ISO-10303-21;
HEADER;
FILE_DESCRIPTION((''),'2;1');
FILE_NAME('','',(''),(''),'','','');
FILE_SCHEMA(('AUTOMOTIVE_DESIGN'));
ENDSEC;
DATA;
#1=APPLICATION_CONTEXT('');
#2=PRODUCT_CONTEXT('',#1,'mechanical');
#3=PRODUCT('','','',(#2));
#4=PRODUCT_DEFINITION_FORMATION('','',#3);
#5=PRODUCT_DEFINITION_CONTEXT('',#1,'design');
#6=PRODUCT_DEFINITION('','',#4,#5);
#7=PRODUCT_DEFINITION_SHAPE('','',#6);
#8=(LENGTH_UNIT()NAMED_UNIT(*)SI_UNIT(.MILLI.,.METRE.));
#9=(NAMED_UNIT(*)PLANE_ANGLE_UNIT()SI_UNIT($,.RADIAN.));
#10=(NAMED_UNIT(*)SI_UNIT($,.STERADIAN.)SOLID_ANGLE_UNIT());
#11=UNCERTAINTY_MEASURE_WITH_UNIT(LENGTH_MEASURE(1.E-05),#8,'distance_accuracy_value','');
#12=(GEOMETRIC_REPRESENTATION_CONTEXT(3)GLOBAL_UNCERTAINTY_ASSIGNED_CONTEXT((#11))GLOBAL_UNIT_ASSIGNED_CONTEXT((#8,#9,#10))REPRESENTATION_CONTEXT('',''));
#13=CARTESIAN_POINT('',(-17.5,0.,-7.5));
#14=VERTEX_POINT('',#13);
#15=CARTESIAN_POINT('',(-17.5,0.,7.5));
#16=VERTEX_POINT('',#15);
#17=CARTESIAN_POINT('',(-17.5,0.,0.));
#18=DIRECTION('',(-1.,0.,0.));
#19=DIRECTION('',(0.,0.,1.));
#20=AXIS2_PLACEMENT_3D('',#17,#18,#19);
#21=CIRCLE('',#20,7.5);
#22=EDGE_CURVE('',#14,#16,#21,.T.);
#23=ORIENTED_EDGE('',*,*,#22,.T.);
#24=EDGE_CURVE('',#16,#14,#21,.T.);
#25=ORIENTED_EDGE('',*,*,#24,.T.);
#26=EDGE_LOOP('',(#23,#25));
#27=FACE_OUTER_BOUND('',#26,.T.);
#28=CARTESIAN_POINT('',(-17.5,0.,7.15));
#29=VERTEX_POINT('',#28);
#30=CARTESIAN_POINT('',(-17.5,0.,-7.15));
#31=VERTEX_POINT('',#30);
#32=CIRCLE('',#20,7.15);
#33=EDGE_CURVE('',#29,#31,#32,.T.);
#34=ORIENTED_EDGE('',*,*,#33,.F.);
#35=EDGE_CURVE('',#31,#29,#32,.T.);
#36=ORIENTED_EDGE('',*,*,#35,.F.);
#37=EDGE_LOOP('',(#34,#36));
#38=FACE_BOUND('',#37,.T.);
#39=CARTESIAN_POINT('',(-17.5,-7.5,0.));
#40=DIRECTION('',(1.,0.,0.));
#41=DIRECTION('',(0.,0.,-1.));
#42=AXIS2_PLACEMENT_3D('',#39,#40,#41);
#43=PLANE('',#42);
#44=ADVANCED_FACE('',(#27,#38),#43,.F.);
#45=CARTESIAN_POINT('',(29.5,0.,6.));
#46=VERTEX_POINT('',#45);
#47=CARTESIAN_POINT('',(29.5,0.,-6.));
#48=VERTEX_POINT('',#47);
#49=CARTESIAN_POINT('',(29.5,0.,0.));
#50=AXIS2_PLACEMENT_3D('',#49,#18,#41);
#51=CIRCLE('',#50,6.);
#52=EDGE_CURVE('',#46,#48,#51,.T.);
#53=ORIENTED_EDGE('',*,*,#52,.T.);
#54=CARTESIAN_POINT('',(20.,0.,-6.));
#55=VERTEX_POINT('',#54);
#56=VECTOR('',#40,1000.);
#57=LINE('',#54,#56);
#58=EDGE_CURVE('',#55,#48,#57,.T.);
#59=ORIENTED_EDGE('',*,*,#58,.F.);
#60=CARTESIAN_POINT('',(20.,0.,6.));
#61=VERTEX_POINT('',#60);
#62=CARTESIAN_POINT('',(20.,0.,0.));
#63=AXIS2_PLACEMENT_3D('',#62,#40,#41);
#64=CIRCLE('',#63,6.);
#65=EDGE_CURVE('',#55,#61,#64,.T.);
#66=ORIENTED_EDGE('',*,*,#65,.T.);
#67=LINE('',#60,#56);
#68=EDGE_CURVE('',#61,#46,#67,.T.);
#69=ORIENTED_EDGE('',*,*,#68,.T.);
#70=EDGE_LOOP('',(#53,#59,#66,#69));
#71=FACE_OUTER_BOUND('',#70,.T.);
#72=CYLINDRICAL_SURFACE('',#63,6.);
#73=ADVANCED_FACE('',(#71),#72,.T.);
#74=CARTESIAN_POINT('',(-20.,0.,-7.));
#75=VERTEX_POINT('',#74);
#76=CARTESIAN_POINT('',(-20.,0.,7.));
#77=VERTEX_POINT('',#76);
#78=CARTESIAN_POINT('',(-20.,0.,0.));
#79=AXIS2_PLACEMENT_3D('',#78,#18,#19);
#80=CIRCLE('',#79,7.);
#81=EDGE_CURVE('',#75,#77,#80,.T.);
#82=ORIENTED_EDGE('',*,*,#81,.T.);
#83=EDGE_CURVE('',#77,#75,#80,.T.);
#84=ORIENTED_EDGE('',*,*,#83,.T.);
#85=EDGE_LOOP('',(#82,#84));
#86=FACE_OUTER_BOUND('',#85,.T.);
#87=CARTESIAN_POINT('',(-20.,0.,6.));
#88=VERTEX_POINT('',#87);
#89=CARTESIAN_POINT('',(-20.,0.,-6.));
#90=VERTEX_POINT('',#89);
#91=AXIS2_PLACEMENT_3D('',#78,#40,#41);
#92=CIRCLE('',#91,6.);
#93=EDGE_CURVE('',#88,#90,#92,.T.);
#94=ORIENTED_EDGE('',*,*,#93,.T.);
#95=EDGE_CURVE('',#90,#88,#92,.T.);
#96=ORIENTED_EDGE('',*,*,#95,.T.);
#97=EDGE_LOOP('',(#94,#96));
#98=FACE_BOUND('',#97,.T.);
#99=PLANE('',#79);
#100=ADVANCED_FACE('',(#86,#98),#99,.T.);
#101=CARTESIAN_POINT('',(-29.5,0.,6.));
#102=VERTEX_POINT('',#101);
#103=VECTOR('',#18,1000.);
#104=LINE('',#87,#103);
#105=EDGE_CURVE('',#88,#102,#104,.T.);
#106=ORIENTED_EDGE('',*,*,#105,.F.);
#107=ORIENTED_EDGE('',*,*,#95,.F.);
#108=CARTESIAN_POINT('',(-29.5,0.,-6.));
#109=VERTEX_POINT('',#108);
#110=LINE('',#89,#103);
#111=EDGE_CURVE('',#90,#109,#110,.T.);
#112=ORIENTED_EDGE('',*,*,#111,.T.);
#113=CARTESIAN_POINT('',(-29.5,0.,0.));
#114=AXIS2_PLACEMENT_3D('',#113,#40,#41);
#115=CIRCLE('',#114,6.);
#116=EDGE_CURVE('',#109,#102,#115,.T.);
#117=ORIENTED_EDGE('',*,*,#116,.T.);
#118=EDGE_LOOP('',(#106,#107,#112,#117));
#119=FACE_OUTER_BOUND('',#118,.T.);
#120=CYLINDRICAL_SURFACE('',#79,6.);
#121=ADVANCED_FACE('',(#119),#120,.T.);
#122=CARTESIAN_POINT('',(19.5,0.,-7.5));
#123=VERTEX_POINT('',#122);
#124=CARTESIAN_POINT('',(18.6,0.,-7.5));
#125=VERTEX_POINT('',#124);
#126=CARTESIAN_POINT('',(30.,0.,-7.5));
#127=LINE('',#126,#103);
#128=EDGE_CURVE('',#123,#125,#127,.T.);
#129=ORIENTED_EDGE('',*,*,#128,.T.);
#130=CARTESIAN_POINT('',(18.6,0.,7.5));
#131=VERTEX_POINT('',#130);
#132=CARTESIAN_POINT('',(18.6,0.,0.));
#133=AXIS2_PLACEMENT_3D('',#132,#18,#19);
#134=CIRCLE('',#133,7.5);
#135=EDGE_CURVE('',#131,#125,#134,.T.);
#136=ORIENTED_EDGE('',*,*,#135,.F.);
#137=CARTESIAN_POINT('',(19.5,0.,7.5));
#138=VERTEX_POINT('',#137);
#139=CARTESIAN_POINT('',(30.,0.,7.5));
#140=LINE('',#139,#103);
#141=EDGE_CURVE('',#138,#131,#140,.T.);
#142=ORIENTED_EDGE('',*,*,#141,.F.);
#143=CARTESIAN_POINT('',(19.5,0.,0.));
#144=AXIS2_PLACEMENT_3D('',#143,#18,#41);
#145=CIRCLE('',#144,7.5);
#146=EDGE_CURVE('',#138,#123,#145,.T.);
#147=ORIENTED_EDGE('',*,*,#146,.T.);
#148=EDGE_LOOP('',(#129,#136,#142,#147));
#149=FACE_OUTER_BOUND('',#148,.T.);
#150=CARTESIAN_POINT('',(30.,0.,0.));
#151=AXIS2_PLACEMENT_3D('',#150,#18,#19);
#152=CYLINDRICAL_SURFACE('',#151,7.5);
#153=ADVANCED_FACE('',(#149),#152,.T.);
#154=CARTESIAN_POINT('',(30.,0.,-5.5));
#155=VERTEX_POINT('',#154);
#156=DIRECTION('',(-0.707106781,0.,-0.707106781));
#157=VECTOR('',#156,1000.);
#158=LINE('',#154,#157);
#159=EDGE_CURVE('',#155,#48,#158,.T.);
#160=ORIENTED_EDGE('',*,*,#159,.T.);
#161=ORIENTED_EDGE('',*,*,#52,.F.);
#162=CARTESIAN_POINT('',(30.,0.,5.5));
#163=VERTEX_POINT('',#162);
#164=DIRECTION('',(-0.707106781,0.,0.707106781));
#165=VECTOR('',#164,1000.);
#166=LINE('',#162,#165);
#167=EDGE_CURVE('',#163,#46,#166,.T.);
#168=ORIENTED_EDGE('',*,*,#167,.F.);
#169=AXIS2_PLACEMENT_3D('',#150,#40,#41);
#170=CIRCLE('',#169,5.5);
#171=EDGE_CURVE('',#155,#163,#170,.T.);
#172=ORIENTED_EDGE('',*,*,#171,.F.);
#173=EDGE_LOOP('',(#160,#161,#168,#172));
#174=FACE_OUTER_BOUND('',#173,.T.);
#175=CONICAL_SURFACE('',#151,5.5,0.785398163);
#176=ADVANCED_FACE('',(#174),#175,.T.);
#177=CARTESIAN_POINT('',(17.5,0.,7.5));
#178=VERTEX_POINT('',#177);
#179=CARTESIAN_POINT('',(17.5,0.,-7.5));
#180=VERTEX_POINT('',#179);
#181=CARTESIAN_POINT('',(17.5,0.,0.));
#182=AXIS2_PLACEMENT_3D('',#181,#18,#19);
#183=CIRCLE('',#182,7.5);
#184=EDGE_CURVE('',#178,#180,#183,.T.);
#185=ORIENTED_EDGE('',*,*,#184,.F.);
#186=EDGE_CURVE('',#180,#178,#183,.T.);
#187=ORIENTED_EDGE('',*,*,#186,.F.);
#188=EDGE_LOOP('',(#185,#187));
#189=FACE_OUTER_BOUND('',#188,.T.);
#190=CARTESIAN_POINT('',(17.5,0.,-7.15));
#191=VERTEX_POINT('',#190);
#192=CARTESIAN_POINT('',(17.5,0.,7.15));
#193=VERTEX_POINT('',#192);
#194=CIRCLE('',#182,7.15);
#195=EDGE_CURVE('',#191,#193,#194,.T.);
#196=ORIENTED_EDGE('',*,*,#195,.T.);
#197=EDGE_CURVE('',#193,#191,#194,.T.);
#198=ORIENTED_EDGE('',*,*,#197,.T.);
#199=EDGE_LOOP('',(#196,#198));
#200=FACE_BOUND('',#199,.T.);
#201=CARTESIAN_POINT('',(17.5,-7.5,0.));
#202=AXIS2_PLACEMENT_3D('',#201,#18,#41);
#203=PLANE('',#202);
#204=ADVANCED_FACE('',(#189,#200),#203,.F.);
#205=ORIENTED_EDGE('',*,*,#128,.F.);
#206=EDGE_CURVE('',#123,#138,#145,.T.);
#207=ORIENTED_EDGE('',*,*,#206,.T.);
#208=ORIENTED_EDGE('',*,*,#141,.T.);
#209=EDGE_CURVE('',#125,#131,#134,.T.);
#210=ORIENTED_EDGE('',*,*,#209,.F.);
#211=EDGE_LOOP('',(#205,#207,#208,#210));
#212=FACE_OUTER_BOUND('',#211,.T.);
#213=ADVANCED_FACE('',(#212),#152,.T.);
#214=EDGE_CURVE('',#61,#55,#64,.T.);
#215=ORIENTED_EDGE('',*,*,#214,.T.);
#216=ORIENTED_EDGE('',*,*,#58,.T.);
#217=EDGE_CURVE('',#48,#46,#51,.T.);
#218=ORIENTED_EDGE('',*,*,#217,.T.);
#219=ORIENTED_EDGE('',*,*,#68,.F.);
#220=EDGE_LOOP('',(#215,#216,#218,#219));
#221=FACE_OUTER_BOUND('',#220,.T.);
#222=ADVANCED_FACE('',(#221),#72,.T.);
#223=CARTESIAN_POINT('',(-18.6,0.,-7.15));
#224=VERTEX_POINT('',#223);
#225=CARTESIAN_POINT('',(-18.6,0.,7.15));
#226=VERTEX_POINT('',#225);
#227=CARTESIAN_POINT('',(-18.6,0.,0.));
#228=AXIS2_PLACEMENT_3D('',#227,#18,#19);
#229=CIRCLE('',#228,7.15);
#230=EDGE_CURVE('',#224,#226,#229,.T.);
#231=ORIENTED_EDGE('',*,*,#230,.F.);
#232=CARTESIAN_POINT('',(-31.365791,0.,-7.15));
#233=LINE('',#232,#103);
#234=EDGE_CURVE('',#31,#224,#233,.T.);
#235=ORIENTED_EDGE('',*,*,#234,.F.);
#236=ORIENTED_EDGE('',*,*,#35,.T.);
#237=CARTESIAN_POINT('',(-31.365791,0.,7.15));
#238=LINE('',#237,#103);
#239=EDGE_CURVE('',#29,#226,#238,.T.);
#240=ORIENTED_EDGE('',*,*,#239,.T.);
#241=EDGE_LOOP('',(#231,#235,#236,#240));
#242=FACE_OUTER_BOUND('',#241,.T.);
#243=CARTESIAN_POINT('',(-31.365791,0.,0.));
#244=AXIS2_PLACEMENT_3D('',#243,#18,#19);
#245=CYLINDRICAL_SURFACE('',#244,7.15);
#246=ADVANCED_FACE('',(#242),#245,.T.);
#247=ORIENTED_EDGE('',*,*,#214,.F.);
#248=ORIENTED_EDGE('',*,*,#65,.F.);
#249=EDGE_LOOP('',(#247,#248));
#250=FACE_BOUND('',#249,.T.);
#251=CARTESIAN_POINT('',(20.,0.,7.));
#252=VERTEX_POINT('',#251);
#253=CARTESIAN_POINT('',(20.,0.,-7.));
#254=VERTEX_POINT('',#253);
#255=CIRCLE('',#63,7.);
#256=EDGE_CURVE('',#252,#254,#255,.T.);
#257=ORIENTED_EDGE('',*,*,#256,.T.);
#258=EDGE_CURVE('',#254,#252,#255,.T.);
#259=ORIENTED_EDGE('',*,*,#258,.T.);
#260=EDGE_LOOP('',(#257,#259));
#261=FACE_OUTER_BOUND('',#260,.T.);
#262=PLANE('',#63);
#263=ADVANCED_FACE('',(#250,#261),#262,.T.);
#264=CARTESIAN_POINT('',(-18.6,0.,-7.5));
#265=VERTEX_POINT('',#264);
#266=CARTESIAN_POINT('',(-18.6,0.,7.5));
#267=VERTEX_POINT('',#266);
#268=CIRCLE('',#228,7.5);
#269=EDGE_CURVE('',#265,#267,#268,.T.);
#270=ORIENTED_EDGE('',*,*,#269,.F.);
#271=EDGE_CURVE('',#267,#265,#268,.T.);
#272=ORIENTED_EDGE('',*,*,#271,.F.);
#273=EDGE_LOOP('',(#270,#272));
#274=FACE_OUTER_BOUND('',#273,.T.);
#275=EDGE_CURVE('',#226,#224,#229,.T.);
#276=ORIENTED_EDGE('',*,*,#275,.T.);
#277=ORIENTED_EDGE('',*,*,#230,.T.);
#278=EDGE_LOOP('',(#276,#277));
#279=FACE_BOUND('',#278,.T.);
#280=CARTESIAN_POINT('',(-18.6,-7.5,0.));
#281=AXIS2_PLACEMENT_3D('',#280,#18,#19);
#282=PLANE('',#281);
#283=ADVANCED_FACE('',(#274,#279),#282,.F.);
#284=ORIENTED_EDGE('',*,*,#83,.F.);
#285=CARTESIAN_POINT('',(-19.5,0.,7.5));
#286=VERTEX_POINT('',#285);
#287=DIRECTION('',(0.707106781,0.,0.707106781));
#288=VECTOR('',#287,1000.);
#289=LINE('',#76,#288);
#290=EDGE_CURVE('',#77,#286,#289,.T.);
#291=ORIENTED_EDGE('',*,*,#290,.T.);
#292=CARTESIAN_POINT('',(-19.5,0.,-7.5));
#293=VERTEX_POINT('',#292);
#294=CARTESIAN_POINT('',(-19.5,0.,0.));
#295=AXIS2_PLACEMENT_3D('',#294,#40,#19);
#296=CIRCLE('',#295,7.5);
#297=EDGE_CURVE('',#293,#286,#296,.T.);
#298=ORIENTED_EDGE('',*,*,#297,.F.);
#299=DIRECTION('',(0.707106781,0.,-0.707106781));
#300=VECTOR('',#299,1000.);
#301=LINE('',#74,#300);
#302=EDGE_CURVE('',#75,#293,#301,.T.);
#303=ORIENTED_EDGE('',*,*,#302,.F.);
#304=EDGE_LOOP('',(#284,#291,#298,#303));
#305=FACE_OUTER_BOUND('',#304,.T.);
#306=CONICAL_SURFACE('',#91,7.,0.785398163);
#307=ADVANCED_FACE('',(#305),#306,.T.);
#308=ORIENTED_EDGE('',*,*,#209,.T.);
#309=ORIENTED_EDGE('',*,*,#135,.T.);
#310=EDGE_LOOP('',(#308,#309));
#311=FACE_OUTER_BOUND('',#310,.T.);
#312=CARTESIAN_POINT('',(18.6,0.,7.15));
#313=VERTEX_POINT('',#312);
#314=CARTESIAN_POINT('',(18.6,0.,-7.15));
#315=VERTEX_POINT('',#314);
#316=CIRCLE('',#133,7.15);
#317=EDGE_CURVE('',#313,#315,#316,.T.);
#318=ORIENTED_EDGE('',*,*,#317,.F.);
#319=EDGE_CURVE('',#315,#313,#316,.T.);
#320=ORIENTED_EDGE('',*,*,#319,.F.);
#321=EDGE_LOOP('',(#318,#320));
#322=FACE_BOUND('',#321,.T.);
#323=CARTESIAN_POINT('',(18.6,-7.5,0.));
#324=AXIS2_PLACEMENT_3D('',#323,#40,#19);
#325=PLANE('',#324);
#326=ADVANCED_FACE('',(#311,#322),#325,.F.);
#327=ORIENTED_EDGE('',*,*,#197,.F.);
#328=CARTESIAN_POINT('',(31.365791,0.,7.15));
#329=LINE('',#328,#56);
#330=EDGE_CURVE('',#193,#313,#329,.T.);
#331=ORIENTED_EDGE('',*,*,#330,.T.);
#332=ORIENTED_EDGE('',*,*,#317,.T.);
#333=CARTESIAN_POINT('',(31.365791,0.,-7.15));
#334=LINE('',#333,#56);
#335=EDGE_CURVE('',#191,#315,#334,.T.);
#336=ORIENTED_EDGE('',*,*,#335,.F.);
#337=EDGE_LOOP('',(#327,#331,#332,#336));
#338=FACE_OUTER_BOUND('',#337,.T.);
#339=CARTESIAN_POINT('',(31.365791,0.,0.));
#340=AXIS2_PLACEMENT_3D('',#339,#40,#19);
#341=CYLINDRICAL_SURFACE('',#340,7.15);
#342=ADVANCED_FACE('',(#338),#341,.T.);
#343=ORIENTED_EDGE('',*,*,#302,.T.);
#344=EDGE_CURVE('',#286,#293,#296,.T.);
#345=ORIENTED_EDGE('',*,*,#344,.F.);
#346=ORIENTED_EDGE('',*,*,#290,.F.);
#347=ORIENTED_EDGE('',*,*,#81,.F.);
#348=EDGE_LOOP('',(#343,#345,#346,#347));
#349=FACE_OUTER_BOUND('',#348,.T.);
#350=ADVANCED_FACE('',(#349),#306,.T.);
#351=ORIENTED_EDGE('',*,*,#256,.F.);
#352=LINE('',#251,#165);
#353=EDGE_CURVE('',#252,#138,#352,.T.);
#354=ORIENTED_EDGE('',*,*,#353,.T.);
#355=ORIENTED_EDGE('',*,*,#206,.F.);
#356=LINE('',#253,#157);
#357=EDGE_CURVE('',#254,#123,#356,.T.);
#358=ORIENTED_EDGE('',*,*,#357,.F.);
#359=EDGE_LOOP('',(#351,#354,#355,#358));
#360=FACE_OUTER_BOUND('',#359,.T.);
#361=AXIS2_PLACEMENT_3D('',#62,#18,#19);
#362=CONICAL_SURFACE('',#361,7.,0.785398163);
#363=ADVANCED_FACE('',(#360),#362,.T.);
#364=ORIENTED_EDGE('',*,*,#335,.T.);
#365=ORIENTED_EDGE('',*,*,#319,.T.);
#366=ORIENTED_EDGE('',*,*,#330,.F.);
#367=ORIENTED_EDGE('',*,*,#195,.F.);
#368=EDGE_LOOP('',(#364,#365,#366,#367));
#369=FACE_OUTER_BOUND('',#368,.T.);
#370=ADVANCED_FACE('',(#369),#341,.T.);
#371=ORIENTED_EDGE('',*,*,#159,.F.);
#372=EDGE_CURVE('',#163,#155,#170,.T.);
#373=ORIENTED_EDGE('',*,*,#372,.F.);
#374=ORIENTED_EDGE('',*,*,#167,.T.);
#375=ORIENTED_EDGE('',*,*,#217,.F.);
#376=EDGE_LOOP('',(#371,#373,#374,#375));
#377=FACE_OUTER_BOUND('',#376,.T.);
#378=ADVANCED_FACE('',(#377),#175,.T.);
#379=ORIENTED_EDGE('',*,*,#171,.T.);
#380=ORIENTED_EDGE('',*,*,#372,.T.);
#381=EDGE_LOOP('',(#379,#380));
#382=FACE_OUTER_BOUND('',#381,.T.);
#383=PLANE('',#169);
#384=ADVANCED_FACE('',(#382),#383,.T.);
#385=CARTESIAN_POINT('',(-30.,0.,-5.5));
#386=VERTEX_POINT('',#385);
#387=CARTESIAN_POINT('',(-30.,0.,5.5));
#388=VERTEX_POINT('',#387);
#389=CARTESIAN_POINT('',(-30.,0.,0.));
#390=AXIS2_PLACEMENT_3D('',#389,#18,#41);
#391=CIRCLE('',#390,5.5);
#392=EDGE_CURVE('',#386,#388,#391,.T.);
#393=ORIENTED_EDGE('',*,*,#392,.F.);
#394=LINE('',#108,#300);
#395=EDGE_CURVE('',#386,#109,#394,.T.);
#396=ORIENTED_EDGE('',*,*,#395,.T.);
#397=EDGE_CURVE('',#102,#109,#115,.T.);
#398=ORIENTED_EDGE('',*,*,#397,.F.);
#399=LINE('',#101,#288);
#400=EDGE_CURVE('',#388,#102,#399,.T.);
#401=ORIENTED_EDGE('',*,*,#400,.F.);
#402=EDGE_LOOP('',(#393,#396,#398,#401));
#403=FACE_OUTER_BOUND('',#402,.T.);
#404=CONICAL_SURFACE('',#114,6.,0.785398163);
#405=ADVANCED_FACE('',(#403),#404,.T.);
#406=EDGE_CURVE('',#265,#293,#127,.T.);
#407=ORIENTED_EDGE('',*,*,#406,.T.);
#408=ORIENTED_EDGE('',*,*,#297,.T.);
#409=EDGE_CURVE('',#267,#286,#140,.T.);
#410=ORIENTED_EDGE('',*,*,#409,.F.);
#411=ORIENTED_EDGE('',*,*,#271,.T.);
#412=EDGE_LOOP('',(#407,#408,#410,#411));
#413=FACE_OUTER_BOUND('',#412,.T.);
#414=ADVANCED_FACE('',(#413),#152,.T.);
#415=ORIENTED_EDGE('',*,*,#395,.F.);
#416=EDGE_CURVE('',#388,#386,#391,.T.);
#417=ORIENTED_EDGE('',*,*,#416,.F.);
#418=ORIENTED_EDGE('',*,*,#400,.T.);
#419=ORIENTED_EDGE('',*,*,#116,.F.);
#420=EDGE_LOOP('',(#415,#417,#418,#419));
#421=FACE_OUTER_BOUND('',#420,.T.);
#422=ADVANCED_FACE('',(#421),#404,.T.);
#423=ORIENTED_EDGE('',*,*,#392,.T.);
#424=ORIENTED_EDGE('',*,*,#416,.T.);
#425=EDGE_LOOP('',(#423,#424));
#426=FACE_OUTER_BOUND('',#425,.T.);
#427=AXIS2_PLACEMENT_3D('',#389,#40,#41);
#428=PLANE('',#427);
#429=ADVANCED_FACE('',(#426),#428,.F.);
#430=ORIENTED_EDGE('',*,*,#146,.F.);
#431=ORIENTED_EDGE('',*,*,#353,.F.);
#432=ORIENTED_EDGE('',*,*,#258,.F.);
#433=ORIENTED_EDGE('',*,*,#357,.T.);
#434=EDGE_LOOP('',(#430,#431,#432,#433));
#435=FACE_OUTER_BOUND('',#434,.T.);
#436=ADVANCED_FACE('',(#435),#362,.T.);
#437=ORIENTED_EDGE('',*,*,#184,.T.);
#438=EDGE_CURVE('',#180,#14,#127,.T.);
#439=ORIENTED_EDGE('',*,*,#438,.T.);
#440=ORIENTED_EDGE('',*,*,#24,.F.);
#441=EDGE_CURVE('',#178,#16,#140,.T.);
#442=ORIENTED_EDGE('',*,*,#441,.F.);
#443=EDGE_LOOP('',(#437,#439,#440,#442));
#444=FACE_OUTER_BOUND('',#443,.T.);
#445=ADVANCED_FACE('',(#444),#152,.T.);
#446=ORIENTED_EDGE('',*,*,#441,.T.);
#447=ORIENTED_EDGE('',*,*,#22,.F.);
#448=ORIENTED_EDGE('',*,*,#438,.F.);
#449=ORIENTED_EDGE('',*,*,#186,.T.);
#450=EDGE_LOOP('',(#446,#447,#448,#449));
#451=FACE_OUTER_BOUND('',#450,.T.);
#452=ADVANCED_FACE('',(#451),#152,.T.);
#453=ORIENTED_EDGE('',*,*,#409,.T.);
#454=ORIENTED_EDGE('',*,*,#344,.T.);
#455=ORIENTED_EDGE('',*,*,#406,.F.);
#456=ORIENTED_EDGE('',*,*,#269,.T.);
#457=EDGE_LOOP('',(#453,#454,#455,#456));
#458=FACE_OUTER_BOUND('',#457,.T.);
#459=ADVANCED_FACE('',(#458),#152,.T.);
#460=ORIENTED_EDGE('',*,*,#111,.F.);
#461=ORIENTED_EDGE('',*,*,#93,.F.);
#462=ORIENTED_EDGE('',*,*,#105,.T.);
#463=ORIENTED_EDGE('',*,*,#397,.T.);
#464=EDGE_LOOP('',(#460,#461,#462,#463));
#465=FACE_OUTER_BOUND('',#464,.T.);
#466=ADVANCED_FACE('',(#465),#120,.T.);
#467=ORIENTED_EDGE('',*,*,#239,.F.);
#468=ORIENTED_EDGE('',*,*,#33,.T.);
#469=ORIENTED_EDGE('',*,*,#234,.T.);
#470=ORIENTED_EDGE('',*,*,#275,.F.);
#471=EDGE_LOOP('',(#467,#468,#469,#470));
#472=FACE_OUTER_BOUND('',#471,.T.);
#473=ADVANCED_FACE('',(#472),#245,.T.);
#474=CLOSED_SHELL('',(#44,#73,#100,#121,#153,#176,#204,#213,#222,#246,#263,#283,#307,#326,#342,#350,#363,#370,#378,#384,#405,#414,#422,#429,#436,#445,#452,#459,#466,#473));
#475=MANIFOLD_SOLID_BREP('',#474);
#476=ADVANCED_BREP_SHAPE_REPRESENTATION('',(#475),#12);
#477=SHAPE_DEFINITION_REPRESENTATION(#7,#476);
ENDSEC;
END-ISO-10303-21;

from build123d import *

# Parameters (mm, degrees)
SKETCH_1_R          = 7.5
EXTRUDE_1_DEPTH     = 30
SKETCH_2_OUTSIDE_W  = 29.728
SKETCH_2_OUTSIDE_H  = 29.728
SKETCH_2_OUTSIDE_R  = 6
CUT_EXTRUDE_1_DEPTH = 10
CHAMFER_1_SIZE      = 0.5
SKETCH_3_W          = 1.1
SKETCH_3_H          = 0.35


with BuildPart() as part:
    # 草图1 → 凸台-拉伸1 (new, symmetric)
    with BuildSketch(Plane(origin=(0, 0, 0), x_dir=(0, 0, -1), z_dir=(1, 0, 0))):
        Circle(SKETCH_1_R)
    extrude(amount=EXTRUDE_1_DEPTH, both=True)

    # 草图2 outside → 切除-拉伸1 (cut)
    with BuildSketch(Plane(origin=(30, 0, 0), x_dir=(0, 0, -1), z_dir=(1, 0, 0))):
        Rectangle(SKETCH_2_OUTSIDE_W, SKETCH_2_OUTSIDE_H)
        Circle(SKETCH_2_OUTSIDE_R, mode=Mode.SUBTRACT)
    cut_extrude_1 = extrude(amount=-CUT_EXTRUDE_1_DEPTH, mode=Mode.SUBTRACT)

    # 镜向1: 切除-拉伸1 across plane
    add(cut_extrude_1.mirror(Plane(origin=(0, 0, 0), x_dir=(0, 0, 1), z_dir=(1, 0, 0))), mode=Mode.SUBTRACT)

    # 倒角1
    chamfer_1_edges = [part.edges().sort_by_distance(p)[0] for p in [
        (30, 0, 6),
        (-30, 0, 6),
        (-20, 0, 7.5),
        (20, 0, 7.5),
    ]]
    chamfer(chamfer_1_edges, length=CHAMFER_1_SIZE)

    # 草图3 → 切除-旋转1 (revolve, cut)
    with BuildSketch(Plane.XY, mode=Mode.PRIVATE) as cut_revolve_1_sk:
        with Locations((-18.05, -7.325)):
            Rectangle(SKETCH_3_W, SKETCH_3_H)
    cut_revolve_1 = revolve(cut_revolve_1_sk.sketch.rotate(Axis((-31.365791293, 0, 0), (1, 0, 0)), 270), axis=Axis((-31.365791293, 0, 0), (1, 0, 0)), mode=Mode.SUBTRACT)

    # 镜向2: 切除-旋转1 across plane
    add(cut_revolve_1.mirror(Plane(origin=(0, 0, 0), x_dir=(0, 0, 1), z_dir=(1, 0, 0))), mode=Mode.SUBTRACT)


solid = part.part
